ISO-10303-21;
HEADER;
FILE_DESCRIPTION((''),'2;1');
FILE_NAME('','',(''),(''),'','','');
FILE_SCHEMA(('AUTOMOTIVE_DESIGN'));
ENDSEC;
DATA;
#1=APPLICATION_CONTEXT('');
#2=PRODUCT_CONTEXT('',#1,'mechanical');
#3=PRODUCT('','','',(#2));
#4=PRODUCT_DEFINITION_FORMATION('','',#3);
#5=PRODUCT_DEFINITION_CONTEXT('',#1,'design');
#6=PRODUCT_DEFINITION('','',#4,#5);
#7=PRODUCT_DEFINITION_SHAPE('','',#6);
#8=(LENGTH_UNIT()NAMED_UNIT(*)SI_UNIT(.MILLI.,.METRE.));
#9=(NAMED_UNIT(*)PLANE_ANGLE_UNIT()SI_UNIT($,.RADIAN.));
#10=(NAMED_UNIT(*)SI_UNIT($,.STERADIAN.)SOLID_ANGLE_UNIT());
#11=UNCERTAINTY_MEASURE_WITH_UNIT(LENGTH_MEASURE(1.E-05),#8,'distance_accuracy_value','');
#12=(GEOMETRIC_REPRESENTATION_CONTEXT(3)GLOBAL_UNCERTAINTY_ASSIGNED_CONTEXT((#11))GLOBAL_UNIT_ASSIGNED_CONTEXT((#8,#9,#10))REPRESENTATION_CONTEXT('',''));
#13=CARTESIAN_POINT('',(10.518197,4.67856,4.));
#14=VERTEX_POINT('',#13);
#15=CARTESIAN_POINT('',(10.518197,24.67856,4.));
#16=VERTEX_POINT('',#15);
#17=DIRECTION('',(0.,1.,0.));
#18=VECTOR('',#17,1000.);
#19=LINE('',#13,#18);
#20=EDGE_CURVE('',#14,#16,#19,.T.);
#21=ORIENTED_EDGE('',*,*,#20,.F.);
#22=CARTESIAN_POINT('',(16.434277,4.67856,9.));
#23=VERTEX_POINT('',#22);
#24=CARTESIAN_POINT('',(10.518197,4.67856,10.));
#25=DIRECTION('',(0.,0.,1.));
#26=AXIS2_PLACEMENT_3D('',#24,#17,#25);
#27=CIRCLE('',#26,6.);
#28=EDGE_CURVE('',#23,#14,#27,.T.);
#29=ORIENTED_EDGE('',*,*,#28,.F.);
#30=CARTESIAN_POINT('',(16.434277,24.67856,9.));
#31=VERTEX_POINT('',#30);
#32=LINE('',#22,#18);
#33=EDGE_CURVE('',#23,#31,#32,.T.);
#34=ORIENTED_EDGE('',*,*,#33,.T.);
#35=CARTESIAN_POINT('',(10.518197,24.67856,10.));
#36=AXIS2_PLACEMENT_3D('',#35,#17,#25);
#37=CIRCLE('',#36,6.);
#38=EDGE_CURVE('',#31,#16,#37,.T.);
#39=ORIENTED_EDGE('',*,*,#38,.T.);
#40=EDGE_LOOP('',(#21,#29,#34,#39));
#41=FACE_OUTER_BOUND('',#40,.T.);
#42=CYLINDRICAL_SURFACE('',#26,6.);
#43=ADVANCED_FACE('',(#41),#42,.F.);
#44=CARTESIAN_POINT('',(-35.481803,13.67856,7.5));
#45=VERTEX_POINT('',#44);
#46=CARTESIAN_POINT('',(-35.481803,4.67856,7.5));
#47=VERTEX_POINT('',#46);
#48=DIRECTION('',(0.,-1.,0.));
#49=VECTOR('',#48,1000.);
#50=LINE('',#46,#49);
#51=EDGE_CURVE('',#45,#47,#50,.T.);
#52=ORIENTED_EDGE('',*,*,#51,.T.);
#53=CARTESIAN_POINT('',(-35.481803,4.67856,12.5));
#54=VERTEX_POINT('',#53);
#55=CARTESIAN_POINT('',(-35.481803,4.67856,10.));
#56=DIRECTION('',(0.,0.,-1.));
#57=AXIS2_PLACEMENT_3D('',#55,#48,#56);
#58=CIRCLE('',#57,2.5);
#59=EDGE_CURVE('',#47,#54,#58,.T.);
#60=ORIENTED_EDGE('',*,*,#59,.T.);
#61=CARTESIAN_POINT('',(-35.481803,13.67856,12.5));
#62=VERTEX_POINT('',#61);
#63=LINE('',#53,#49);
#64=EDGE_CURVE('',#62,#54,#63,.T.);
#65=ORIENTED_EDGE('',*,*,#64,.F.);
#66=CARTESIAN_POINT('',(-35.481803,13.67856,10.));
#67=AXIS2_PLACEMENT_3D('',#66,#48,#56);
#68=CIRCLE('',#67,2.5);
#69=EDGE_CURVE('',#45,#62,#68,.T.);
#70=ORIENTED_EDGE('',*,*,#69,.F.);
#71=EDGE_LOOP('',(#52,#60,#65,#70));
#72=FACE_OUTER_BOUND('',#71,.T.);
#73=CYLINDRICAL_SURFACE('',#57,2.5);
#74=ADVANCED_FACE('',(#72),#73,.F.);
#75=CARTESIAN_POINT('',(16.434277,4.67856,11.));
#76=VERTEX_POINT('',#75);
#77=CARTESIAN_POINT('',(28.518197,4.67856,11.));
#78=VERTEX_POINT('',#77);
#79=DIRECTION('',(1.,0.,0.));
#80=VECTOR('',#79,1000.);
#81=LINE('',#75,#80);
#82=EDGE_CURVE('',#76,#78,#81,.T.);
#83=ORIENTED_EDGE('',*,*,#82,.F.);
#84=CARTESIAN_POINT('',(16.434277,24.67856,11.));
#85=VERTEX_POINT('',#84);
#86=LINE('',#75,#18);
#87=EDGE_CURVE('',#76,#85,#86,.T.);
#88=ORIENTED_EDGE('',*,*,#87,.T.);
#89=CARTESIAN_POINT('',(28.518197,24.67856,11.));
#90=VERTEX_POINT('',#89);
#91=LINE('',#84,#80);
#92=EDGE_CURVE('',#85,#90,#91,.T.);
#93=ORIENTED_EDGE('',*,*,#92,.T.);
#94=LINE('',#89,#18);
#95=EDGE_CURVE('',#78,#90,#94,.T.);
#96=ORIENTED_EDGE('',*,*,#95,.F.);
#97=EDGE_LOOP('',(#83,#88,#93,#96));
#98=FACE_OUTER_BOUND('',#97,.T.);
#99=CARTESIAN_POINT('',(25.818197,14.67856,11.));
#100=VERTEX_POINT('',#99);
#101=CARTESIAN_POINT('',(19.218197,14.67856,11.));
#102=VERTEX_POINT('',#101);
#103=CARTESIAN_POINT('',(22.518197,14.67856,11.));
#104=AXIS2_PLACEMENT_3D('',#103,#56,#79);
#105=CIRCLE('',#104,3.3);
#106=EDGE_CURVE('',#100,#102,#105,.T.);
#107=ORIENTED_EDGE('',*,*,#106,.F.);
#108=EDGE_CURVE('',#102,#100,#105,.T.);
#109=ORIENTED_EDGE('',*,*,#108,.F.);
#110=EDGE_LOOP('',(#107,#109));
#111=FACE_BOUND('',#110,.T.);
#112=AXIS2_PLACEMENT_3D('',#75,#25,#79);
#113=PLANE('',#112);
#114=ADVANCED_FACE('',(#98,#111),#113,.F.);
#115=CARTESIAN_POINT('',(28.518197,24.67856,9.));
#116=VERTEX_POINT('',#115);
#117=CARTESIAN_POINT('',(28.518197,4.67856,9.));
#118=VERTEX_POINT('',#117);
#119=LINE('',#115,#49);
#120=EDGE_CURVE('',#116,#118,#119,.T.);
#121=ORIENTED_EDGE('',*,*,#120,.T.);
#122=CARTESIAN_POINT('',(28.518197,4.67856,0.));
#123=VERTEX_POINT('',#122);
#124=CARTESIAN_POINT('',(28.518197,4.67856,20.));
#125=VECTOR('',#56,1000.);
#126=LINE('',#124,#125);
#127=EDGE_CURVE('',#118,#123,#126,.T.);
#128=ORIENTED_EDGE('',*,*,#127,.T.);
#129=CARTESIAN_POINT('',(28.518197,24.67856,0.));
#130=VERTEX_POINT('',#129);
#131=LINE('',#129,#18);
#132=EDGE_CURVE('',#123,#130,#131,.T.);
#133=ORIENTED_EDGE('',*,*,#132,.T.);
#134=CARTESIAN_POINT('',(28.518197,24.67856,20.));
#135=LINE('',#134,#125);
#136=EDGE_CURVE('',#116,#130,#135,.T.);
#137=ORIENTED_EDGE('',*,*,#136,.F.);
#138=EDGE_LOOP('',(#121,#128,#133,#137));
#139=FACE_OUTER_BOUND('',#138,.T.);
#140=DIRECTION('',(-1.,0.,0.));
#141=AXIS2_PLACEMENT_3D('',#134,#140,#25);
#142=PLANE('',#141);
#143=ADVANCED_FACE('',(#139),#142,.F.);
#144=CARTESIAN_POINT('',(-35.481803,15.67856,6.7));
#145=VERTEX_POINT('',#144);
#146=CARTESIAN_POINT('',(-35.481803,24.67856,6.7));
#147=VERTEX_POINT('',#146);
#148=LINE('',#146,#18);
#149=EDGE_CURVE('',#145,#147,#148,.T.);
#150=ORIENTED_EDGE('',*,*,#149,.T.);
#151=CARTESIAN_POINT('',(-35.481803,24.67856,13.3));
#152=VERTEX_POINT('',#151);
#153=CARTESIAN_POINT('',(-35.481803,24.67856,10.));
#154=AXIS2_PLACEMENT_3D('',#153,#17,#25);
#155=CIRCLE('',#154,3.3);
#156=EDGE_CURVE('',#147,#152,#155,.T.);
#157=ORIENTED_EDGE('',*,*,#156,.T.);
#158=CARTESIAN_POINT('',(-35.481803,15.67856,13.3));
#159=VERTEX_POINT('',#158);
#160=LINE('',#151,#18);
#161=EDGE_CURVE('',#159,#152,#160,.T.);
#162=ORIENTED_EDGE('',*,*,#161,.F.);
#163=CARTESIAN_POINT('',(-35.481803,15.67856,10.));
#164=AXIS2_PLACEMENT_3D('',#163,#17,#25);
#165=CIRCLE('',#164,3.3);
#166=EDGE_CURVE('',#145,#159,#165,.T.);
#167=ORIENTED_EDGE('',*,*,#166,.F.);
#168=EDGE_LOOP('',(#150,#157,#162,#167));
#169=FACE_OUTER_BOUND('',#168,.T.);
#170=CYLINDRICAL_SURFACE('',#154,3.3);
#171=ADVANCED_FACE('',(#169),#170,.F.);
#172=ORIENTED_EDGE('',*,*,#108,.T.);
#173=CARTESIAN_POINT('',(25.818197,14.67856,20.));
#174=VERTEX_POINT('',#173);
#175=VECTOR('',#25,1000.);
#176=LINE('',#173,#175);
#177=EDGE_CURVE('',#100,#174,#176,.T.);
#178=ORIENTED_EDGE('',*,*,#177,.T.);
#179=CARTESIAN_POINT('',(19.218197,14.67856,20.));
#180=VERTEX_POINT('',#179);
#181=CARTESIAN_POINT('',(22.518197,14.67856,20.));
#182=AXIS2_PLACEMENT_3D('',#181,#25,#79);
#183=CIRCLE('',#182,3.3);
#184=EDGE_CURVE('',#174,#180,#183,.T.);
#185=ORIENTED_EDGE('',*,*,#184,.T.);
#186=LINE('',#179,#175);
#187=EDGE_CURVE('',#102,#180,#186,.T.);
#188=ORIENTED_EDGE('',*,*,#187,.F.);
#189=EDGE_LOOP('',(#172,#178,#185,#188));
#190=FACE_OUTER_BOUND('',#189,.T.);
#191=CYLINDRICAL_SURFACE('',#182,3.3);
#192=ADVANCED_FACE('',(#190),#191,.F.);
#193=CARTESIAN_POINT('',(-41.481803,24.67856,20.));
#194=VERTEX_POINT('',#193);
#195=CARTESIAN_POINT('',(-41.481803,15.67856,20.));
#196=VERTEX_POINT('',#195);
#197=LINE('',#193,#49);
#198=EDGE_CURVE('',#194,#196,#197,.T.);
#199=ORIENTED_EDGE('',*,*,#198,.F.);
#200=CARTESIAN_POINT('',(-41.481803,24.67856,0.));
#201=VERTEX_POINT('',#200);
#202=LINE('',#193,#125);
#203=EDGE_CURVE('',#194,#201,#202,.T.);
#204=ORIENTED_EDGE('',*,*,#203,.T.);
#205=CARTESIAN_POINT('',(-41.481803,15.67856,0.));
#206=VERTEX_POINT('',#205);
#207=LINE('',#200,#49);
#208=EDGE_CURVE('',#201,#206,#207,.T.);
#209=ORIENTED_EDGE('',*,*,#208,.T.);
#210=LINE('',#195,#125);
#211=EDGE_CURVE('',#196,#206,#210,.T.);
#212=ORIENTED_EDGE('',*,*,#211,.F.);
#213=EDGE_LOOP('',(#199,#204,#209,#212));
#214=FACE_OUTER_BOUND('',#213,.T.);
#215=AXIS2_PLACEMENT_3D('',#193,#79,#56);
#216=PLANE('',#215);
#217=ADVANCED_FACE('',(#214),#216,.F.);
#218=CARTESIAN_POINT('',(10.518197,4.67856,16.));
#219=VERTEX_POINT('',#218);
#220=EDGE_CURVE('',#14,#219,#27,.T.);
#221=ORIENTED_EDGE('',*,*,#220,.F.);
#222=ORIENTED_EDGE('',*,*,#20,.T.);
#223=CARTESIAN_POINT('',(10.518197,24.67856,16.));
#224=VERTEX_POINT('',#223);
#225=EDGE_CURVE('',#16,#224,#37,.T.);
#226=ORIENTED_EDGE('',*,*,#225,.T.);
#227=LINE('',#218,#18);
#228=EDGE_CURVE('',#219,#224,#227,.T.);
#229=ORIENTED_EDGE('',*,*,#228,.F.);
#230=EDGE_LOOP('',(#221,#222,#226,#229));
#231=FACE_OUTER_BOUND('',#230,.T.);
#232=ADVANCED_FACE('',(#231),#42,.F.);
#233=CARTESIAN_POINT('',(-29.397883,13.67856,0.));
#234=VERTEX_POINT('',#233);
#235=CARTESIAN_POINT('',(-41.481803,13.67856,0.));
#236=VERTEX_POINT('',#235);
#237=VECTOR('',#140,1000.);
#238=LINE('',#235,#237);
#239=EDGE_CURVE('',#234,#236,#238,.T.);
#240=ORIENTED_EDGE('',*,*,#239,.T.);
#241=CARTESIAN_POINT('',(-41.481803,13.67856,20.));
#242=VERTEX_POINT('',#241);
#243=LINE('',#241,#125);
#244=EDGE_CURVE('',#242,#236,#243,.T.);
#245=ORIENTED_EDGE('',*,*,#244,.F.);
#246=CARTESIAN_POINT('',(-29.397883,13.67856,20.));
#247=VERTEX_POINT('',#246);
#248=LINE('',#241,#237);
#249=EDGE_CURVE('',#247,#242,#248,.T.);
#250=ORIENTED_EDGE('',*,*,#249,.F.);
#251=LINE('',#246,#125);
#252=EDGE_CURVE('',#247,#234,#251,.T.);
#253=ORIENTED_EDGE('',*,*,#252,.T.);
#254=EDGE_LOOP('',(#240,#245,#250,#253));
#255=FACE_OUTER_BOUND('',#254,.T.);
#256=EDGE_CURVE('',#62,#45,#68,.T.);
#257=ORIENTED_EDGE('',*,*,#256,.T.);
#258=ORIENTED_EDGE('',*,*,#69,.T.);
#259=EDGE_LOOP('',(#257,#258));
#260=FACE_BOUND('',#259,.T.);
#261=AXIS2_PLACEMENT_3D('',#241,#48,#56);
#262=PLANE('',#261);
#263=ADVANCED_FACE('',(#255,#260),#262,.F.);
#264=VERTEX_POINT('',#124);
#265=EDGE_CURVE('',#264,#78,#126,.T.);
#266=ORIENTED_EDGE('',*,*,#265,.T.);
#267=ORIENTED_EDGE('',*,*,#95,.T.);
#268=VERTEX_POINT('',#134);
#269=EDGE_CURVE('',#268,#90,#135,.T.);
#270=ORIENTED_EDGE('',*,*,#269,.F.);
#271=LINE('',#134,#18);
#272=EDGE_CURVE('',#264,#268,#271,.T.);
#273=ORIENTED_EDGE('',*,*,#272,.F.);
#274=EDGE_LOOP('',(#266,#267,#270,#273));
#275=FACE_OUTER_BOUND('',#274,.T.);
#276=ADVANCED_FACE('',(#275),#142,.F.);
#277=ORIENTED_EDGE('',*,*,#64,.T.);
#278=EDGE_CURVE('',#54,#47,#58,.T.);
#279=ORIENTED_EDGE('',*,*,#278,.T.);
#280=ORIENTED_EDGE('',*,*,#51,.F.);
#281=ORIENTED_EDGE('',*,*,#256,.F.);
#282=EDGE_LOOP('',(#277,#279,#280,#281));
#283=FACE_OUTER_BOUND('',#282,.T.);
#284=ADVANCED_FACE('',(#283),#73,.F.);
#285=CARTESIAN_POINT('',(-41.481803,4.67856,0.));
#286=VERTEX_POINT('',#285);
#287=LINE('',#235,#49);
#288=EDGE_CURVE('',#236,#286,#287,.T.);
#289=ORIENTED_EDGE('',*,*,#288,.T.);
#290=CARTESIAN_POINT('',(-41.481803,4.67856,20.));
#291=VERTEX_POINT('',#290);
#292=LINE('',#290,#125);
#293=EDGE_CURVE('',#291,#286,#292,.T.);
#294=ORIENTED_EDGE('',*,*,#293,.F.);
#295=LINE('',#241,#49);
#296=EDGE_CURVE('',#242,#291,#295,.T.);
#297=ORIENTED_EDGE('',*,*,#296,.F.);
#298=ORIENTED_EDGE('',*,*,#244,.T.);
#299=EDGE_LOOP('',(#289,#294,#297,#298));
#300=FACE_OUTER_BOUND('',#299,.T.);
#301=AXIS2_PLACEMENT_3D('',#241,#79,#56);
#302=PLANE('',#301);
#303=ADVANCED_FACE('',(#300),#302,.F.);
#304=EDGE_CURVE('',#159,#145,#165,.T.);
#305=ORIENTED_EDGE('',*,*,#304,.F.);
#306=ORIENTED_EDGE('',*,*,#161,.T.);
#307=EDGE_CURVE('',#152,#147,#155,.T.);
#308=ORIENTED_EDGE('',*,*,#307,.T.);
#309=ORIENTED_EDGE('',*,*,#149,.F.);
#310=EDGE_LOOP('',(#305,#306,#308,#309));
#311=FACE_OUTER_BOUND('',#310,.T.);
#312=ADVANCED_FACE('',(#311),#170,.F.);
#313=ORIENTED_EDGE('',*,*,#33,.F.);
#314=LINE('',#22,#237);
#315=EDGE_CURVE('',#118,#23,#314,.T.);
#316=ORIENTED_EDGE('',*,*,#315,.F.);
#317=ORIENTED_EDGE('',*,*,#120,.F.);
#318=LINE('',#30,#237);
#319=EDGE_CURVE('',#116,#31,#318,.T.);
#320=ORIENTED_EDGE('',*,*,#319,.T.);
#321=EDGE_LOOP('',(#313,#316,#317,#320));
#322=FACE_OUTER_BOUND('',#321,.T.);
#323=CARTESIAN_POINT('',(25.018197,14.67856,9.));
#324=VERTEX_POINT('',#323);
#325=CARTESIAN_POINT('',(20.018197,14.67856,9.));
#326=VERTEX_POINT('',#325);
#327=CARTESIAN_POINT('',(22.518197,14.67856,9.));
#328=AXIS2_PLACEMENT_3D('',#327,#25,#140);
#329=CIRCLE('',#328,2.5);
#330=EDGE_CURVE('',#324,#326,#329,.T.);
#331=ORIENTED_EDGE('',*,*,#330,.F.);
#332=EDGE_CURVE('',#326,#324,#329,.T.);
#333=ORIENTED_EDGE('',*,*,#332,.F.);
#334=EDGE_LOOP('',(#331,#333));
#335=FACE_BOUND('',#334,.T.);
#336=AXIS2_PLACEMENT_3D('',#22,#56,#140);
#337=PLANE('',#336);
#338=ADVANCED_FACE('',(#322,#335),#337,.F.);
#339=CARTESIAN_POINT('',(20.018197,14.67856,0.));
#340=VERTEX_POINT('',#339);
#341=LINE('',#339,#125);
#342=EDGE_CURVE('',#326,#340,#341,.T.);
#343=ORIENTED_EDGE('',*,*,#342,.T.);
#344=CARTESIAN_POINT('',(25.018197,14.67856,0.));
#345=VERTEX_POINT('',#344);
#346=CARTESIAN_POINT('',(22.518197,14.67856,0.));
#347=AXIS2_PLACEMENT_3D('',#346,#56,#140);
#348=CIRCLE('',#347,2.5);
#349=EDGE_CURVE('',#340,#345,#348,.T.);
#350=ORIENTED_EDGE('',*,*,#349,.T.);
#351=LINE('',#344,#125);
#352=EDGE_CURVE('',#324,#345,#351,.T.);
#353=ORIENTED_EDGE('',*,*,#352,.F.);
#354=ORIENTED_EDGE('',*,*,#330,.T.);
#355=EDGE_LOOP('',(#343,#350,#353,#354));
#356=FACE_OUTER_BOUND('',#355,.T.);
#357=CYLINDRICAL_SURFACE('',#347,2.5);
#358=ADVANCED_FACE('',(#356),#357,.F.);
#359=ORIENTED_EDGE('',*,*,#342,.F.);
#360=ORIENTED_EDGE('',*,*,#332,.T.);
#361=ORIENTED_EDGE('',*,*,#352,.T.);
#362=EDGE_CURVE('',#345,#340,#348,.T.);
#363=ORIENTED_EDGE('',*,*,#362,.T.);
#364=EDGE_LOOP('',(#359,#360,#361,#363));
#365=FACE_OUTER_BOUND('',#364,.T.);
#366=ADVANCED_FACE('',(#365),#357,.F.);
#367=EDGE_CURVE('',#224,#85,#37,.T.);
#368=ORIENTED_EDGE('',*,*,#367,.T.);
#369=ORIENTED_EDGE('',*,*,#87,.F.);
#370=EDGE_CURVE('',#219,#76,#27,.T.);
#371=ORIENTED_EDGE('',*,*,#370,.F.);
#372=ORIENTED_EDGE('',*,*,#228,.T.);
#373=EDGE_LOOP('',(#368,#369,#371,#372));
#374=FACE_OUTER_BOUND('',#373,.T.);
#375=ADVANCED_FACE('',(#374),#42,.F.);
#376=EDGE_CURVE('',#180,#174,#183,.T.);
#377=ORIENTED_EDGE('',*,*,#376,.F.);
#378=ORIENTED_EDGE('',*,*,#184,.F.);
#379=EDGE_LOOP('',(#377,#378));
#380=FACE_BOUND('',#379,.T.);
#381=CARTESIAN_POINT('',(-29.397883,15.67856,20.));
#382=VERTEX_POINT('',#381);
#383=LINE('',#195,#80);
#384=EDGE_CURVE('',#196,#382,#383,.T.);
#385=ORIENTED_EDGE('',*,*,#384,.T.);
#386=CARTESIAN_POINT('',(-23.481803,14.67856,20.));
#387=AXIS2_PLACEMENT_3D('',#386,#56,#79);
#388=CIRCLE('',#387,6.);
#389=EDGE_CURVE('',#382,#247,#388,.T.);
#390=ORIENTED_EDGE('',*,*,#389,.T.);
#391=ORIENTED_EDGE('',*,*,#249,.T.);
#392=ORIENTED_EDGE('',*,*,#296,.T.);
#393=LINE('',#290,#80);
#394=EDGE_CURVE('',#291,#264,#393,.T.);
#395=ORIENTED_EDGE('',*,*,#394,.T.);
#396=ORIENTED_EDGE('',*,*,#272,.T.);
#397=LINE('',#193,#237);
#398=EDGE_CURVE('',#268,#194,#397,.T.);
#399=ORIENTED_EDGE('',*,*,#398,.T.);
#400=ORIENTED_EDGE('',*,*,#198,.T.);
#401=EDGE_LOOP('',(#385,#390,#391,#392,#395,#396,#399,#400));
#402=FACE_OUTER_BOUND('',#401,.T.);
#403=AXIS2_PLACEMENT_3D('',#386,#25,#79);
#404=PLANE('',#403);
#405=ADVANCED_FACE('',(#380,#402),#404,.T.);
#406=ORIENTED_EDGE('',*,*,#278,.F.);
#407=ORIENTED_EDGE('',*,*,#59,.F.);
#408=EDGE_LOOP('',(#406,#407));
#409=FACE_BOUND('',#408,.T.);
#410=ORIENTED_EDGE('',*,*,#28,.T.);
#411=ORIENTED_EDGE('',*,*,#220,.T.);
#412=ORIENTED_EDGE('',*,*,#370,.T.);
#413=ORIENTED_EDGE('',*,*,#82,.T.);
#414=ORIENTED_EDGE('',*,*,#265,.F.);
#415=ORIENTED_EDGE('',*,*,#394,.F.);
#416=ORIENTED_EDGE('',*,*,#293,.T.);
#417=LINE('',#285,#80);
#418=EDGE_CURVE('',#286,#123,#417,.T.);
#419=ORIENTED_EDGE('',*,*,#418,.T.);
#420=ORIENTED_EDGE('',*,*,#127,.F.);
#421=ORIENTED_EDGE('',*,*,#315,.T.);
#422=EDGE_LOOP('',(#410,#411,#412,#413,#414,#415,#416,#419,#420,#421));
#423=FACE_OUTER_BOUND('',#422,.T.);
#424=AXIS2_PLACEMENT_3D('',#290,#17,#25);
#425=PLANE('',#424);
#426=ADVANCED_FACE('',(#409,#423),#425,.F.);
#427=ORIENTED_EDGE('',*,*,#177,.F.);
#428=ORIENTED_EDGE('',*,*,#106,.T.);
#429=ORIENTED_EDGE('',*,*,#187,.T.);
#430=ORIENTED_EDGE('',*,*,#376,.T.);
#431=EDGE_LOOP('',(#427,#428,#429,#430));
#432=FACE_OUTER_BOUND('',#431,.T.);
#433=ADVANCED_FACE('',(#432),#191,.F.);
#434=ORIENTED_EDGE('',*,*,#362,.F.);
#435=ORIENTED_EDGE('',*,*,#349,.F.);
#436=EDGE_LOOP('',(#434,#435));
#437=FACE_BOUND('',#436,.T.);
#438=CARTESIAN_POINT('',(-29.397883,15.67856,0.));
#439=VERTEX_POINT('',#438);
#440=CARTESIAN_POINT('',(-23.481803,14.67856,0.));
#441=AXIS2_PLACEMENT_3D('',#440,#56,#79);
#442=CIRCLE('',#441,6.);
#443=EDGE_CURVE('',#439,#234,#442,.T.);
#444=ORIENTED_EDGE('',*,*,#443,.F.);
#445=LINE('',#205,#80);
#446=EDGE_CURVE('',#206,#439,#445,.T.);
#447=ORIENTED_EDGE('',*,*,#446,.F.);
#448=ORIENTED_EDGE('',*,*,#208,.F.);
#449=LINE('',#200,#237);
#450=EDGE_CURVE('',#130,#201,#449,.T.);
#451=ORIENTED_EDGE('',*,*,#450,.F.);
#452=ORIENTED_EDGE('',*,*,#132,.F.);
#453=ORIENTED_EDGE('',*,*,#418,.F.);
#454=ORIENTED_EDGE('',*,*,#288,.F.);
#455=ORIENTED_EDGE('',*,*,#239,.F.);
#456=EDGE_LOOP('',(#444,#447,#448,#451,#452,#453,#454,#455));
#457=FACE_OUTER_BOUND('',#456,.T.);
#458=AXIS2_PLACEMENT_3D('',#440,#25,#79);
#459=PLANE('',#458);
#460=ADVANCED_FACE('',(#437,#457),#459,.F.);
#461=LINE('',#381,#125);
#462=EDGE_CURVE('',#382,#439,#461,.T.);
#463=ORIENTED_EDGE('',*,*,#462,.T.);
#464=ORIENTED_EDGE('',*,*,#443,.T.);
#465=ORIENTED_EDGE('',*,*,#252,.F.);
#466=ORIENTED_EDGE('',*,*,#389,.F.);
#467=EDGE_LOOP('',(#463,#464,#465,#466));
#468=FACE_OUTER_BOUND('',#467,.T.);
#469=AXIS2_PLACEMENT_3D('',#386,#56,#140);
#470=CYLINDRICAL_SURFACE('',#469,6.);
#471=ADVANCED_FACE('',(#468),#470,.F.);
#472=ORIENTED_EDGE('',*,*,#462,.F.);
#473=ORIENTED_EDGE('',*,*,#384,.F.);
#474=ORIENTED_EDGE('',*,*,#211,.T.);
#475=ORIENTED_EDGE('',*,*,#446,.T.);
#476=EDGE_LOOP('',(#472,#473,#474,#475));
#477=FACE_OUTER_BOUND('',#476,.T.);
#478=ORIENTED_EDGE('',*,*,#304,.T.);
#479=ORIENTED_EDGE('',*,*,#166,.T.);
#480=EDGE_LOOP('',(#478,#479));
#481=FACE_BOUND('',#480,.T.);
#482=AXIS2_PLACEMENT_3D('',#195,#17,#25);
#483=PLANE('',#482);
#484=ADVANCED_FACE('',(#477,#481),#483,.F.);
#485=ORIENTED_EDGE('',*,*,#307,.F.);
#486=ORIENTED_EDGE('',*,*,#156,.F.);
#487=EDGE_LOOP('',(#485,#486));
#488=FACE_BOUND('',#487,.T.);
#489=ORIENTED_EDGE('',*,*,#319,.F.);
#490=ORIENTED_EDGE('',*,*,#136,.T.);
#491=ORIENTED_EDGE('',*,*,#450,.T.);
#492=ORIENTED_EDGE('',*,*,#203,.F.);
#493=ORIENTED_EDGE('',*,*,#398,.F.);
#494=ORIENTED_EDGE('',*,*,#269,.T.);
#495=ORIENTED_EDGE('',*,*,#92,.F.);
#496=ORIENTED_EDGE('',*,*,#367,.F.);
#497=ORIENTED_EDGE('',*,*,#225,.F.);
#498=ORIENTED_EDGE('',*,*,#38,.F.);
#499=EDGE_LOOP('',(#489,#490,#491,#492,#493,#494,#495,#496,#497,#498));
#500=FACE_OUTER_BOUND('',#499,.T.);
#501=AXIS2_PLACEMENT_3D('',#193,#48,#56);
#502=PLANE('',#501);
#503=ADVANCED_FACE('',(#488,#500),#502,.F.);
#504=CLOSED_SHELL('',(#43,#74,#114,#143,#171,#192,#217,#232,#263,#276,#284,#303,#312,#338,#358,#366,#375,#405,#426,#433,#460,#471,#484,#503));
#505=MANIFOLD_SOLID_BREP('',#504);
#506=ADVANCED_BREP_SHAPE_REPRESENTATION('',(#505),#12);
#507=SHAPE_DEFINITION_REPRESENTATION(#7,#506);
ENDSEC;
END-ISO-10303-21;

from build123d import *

# Parameters (mm, degrees)
SKETCH1_R             = 2
BOSS_EXTRUDE1_DEPTH   = 20
HOLE1_D               = 6.6
HOLE1_DEPTH           = 9
M6_TAPPED_HOLE1_D     = 5
M6_TAPPED_HOLE1_DEPTH = 9
M6_TAPPED_HOLE1_TIP   = 1.502151548
SKETCH6_R             = 2
CUT_EXTRUDE1_DEPTH    = 51.206971578
M6_TAPPED_HOLE2_D     = 5
M6_TAPPED_HOLE2_DEPTH = 9
M6_TAPPED_HOLE2_TIP   = 1.502151548
HOLE2_D               = 6.6
HOLE2_DEPTH           = 9


with BuildPart() as part:
    # Sketch1 → Boss-Extrude1 (new body)
    with BuildSketch(Plane.XY):
        with BuildLine():
            Line((-41.48180318, 24.678559646), (28.51819682, 24.678559646))
            Line((28.51819682, 24.678559646), (28.51819682, 4.678559646))
            Line((28.51819682, 4.678559646), (-41.48180318, 4.678559646))
            Line((-41.48180318, 4.678559646), (-41.48180318, 13.678559646))
            Line((-41.48180318, 13.678559646), (-29.397882963, 13.678559646))
            ThreePointArc((-29.397882963, 13.678559646), (-17.48180318, 14.678559646), (-29.397882963, 15.678559646))
            Line((-29.397882963, 15.678559646), (-41.48180318, 15.678559646))
            Line((-41.48180318, 15.678559646), (-41.48180318, 24.678559646))
        make_face()
        with Locations((22.51819682, 14.678559646)):
            Circle(SKETCH1_R, mode=Mode.SUBTRACT)
    extrude(amount=BOSS_EXTRUDE1_DEPTH)

    # Hole1
    with Locations(Plane.XY.offset(20)):
        with Locations((22.51819682, 14.678559646)):
            Hole(HOLE1_D / 2, depth=HOLE1_DEPTH)

    # M6 Tapped Hole1
    with Locations(Plane(origin=(0, 0, 0), x_dir=(-1, 0, 0), z_dir=(0, 0, -1))):
        with Locations((-22.51819682, 14.678559646)):
            Hole(M6_TAPPED_HOLE1_D / 2, depth=M6_TAPPED_HOLE1_DEPTH)
            with Locations((0, 0, -(M6_TAPPED_HOLE1_DEPTH + M6_TAPPED_HOLE1_TIP / 2))):  # 118° drill point
                Cone(0, M6_TAPPED_HOLE1_D / 2, M6_TAPPED_HOLE1_TIP, mode=Mode.SUBTRACT)

    # Sketch6 → Cut-Extrude1 (cut, through all)
    with BuildSketch(Plane(origin=(0, 24.678559646, 0), x_dir=(1, 0, 0), z_dir=(0, 1, 0))):
        with Locations(Location((-35.48180318, -10, 0), (0, 0, 270))):
            Circle(SKETCH6_R)
        with BuildLine():
            Line((16.434276603, -11), (30.650689968, -11))
            Line((30.650689968, -11), (30.650689968, -9))
            Line((30.650689968, -9), (16.434276603, -9))
            ThreePointArc((16.434276603, -9), (4.51819682, -10), (16.434276603, -11))
        make_face()
    extrude(amount=-CUT_EXTRUDE1_DEPTH, mode=Mode.SUBTRACT)

    # M6 Tapped Hole2
    with Locations(Plane(origin=(0, 4.678559646, 0), x_dir=(-1, 0, 0), z_dir=(0, -1, 0))):
        with Locations((35.48180318, -10)):
            Hole(M6_TAPPED_HOLE2_D / 2, depth=M6_TAPPED_HOLE2_DEPTH)
            with Locations((0, 0, -(M6_TAPPED_HOLE2_DEPTH + M6_TAPPED_HOLE2_TIP / 2))):  # 118° drill point
                Cone(0, M6_TAPPED_HOLE2_D / 2, M6_TAPPED_HOLE2_TIP, mode=Mode.SUBTRACT)

    # Hole2
    with Locations(Plane(origin=(0, 24.678559646, 0), x_dir=(1, 0, 0), z_dir=(0, 1, 0))):
        with Locations((-35.48180318, -10)):
            Hole(HOLE2_D / 2, depth=HOLE2_DEPTH)


solid = part.part
